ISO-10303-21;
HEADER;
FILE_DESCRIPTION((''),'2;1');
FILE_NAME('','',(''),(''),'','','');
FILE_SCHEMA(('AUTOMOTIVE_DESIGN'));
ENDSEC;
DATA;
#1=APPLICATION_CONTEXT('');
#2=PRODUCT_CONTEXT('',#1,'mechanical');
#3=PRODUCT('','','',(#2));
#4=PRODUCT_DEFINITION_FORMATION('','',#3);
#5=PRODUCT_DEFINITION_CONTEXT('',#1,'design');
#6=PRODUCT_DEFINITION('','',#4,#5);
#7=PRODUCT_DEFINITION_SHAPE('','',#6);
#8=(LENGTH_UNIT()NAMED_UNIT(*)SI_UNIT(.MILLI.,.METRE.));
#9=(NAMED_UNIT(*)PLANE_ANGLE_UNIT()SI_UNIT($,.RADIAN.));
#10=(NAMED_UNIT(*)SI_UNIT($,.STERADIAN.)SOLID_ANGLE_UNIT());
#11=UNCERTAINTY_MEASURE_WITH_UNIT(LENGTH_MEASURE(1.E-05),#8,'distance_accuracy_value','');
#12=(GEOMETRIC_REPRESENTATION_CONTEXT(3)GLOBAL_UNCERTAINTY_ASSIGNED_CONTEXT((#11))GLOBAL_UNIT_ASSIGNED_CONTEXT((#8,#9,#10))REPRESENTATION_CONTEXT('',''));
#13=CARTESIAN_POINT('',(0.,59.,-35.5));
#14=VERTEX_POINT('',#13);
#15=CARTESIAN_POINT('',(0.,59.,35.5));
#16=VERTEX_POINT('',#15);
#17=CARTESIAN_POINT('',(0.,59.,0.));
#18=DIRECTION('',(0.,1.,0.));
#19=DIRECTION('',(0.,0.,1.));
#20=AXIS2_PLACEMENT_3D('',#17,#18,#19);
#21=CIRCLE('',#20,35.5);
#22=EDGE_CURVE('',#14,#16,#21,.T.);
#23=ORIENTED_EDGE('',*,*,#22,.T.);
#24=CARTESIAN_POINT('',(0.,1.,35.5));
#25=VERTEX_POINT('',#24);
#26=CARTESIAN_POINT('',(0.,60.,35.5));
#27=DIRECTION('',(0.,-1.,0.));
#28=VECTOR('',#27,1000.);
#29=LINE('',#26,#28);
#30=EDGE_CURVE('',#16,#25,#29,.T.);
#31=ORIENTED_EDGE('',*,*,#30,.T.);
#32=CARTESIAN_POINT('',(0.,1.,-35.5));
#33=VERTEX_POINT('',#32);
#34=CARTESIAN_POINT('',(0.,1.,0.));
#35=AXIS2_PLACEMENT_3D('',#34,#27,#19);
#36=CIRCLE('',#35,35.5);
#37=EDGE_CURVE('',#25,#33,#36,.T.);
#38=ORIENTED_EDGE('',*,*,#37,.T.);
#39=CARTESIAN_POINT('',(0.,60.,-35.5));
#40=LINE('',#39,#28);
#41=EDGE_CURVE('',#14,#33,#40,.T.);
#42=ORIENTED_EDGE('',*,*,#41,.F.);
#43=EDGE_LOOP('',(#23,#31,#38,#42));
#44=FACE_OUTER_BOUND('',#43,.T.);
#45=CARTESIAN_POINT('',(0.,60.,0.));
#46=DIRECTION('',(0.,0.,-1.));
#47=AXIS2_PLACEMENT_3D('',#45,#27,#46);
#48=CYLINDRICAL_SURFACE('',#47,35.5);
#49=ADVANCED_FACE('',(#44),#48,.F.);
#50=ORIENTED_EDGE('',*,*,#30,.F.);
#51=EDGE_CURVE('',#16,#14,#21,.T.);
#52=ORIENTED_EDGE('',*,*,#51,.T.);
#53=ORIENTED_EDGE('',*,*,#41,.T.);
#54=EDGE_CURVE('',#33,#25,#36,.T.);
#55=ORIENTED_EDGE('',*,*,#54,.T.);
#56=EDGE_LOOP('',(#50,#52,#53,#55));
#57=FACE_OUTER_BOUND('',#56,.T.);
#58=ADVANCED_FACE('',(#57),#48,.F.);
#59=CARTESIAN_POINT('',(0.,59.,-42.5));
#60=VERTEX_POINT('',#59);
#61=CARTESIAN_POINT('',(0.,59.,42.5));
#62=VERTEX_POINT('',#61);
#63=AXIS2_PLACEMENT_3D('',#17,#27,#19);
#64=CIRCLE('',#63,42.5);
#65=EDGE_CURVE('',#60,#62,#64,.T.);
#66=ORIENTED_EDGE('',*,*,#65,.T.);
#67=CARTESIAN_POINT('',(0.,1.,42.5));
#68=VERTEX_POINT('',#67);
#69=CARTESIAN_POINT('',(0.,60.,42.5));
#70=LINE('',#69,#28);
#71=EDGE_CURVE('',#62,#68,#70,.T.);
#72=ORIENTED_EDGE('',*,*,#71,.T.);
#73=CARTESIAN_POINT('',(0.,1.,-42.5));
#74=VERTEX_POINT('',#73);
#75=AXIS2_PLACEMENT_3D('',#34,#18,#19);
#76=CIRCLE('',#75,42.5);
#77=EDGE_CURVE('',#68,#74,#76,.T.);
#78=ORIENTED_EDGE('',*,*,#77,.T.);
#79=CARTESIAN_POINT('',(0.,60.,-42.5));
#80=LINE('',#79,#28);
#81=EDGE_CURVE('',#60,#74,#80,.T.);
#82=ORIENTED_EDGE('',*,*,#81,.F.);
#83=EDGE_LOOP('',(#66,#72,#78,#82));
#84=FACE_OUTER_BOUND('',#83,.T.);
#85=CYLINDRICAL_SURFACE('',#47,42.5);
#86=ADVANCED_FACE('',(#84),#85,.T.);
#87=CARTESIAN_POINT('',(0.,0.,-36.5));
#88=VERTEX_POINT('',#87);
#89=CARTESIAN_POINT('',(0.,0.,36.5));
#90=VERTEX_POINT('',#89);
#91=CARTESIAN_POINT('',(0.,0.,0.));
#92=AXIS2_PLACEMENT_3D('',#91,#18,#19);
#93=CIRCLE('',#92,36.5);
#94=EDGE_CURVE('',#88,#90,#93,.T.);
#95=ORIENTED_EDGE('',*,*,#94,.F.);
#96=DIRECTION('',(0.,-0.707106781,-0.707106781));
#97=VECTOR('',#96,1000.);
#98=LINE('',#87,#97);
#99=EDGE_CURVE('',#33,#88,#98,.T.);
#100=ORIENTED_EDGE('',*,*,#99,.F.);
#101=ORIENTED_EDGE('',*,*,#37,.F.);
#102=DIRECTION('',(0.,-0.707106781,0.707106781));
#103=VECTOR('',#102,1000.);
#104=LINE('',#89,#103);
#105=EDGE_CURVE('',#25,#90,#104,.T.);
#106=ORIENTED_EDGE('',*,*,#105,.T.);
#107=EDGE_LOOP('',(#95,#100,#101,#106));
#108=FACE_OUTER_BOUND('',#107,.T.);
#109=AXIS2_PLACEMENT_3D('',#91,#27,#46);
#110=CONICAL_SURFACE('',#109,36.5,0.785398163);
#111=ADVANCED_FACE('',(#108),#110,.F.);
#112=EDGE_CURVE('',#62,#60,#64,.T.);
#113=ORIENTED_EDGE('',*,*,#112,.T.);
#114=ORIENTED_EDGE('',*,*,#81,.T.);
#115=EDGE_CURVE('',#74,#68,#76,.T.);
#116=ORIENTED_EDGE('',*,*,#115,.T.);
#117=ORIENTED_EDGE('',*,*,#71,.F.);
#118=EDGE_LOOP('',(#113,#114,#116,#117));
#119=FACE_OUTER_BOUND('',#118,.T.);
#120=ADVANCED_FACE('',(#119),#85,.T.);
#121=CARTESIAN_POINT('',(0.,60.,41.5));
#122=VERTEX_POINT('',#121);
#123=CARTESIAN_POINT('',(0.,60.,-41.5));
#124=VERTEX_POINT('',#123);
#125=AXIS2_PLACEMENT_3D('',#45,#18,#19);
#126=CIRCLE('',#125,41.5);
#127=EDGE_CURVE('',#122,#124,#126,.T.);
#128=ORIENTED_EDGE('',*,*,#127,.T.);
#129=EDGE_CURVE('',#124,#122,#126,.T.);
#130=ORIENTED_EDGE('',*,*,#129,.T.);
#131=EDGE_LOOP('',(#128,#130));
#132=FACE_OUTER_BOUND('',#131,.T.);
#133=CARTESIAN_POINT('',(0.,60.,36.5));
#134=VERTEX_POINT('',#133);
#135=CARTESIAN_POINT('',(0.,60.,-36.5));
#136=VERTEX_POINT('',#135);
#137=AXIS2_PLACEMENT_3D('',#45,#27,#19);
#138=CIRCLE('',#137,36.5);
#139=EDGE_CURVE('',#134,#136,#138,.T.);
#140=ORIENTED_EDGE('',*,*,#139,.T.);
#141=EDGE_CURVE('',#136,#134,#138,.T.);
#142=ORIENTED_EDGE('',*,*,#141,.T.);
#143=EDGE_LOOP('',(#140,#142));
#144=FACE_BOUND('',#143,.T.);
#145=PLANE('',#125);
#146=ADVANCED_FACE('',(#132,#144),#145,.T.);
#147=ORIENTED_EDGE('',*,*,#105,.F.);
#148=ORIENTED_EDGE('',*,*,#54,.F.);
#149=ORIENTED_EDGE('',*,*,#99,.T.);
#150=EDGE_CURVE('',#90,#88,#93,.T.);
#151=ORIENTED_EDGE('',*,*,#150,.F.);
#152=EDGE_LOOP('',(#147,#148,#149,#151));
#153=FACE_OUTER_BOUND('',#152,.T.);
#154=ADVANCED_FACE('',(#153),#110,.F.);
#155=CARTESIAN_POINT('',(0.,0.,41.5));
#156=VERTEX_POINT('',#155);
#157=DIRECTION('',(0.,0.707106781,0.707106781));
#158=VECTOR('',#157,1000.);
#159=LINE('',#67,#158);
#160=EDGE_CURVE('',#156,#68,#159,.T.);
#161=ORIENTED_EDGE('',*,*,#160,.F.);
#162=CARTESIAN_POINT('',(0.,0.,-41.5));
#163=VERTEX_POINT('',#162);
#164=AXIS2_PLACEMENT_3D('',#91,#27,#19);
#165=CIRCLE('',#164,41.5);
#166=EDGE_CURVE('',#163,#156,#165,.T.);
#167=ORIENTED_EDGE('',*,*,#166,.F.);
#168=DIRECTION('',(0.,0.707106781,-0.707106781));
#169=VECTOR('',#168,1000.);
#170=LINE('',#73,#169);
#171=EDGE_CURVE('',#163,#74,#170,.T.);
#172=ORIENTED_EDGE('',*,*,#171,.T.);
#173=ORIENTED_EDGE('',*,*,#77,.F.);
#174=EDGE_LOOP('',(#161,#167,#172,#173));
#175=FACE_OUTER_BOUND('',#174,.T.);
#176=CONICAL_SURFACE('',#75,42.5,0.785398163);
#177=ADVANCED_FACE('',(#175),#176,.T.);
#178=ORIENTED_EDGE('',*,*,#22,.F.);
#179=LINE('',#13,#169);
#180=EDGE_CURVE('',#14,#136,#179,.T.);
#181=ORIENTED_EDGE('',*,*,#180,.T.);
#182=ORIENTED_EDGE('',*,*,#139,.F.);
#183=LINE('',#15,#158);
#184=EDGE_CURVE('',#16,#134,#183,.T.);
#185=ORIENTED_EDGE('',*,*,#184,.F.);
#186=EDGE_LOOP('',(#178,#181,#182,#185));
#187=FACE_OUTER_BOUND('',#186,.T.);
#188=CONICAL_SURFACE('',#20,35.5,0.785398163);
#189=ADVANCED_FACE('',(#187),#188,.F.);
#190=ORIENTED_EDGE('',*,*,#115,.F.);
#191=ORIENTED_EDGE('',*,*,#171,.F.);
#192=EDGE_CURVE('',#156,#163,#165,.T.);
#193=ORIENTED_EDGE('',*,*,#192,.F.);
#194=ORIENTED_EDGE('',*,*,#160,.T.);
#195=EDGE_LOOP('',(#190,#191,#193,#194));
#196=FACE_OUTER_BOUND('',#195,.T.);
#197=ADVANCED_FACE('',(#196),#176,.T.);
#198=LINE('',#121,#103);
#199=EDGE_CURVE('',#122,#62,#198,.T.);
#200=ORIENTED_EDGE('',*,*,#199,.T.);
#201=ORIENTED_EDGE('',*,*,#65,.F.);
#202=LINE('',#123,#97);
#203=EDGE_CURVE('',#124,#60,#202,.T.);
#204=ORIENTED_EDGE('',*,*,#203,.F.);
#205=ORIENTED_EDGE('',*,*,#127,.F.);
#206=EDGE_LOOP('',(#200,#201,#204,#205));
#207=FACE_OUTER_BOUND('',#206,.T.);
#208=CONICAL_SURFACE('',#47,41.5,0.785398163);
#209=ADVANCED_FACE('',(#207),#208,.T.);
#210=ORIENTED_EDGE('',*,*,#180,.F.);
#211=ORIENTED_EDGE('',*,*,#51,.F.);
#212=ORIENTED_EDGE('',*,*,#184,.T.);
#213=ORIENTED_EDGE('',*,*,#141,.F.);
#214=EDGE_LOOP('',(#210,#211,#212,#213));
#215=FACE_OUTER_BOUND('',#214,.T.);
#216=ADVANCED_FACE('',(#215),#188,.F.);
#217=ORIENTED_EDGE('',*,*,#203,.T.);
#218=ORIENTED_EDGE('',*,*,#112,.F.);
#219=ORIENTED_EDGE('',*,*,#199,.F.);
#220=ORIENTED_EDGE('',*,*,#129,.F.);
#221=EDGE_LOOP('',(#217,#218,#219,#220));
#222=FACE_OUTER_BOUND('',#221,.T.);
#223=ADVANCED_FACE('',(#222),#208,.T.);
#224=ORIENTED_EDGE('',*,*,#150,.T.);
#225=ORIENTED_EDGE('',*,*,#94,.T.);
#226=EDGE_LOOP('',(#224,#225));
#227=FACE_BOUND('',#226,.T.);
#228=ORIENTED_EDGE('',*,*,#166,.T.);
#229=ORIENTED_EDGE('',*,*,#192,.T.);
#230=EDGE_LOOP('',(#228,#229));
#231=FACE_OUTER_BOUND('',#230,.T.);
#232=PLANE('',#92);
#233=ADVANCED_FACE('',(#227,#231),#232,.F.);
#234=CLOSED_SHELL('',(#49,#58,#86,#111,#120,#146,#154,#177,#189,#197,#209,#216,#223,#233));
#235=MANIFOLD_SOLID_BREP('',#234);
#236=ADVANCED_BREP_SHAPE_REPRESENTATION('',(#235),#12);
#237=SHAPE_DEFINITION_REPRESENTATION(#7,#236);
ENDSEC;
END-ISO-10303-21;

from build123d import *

# Parameters (mm, degrees)
SKETCH1_R           = 42.5
SKETCH1_R_2         = 35.5
BOSS_EXTRUDE1_DEPTH = 60
CHAMFER2_SIZE       = 1


with BuildPart() as part:
    # Sketch1 → Boss-Extrude1 (new body)
    with BuildSketch(Plane(origin=(0, 0, 0), x_dir=(1, 0, 0), z_dir=(0, 1, 0))):
        with Locations(Location((0, 0, 0), (0, 0, 270))):
            Circle(SKETCH1_R)
        with Locations(Location((0, 0, 0), (0, 0, 270))):
            Circle(SKETCH1_R_2, mode=Mode.SUBTRACT)
    extrude(amount=BOSS_EXTRUDE1_DEPTH)

    # Chamfer2
    chamfer2_edges = [part.edges().sort_by_distance(p)[0] for p in [
        (0, 0, -42.5),
        (0, 60, -42.5),
        (0, 0, -35.5),
        (0, 60, -35.5),
    ]]
    chamfer(chamfer2_edges, length=CHAMFER2_SIZE)


solid = part.part
